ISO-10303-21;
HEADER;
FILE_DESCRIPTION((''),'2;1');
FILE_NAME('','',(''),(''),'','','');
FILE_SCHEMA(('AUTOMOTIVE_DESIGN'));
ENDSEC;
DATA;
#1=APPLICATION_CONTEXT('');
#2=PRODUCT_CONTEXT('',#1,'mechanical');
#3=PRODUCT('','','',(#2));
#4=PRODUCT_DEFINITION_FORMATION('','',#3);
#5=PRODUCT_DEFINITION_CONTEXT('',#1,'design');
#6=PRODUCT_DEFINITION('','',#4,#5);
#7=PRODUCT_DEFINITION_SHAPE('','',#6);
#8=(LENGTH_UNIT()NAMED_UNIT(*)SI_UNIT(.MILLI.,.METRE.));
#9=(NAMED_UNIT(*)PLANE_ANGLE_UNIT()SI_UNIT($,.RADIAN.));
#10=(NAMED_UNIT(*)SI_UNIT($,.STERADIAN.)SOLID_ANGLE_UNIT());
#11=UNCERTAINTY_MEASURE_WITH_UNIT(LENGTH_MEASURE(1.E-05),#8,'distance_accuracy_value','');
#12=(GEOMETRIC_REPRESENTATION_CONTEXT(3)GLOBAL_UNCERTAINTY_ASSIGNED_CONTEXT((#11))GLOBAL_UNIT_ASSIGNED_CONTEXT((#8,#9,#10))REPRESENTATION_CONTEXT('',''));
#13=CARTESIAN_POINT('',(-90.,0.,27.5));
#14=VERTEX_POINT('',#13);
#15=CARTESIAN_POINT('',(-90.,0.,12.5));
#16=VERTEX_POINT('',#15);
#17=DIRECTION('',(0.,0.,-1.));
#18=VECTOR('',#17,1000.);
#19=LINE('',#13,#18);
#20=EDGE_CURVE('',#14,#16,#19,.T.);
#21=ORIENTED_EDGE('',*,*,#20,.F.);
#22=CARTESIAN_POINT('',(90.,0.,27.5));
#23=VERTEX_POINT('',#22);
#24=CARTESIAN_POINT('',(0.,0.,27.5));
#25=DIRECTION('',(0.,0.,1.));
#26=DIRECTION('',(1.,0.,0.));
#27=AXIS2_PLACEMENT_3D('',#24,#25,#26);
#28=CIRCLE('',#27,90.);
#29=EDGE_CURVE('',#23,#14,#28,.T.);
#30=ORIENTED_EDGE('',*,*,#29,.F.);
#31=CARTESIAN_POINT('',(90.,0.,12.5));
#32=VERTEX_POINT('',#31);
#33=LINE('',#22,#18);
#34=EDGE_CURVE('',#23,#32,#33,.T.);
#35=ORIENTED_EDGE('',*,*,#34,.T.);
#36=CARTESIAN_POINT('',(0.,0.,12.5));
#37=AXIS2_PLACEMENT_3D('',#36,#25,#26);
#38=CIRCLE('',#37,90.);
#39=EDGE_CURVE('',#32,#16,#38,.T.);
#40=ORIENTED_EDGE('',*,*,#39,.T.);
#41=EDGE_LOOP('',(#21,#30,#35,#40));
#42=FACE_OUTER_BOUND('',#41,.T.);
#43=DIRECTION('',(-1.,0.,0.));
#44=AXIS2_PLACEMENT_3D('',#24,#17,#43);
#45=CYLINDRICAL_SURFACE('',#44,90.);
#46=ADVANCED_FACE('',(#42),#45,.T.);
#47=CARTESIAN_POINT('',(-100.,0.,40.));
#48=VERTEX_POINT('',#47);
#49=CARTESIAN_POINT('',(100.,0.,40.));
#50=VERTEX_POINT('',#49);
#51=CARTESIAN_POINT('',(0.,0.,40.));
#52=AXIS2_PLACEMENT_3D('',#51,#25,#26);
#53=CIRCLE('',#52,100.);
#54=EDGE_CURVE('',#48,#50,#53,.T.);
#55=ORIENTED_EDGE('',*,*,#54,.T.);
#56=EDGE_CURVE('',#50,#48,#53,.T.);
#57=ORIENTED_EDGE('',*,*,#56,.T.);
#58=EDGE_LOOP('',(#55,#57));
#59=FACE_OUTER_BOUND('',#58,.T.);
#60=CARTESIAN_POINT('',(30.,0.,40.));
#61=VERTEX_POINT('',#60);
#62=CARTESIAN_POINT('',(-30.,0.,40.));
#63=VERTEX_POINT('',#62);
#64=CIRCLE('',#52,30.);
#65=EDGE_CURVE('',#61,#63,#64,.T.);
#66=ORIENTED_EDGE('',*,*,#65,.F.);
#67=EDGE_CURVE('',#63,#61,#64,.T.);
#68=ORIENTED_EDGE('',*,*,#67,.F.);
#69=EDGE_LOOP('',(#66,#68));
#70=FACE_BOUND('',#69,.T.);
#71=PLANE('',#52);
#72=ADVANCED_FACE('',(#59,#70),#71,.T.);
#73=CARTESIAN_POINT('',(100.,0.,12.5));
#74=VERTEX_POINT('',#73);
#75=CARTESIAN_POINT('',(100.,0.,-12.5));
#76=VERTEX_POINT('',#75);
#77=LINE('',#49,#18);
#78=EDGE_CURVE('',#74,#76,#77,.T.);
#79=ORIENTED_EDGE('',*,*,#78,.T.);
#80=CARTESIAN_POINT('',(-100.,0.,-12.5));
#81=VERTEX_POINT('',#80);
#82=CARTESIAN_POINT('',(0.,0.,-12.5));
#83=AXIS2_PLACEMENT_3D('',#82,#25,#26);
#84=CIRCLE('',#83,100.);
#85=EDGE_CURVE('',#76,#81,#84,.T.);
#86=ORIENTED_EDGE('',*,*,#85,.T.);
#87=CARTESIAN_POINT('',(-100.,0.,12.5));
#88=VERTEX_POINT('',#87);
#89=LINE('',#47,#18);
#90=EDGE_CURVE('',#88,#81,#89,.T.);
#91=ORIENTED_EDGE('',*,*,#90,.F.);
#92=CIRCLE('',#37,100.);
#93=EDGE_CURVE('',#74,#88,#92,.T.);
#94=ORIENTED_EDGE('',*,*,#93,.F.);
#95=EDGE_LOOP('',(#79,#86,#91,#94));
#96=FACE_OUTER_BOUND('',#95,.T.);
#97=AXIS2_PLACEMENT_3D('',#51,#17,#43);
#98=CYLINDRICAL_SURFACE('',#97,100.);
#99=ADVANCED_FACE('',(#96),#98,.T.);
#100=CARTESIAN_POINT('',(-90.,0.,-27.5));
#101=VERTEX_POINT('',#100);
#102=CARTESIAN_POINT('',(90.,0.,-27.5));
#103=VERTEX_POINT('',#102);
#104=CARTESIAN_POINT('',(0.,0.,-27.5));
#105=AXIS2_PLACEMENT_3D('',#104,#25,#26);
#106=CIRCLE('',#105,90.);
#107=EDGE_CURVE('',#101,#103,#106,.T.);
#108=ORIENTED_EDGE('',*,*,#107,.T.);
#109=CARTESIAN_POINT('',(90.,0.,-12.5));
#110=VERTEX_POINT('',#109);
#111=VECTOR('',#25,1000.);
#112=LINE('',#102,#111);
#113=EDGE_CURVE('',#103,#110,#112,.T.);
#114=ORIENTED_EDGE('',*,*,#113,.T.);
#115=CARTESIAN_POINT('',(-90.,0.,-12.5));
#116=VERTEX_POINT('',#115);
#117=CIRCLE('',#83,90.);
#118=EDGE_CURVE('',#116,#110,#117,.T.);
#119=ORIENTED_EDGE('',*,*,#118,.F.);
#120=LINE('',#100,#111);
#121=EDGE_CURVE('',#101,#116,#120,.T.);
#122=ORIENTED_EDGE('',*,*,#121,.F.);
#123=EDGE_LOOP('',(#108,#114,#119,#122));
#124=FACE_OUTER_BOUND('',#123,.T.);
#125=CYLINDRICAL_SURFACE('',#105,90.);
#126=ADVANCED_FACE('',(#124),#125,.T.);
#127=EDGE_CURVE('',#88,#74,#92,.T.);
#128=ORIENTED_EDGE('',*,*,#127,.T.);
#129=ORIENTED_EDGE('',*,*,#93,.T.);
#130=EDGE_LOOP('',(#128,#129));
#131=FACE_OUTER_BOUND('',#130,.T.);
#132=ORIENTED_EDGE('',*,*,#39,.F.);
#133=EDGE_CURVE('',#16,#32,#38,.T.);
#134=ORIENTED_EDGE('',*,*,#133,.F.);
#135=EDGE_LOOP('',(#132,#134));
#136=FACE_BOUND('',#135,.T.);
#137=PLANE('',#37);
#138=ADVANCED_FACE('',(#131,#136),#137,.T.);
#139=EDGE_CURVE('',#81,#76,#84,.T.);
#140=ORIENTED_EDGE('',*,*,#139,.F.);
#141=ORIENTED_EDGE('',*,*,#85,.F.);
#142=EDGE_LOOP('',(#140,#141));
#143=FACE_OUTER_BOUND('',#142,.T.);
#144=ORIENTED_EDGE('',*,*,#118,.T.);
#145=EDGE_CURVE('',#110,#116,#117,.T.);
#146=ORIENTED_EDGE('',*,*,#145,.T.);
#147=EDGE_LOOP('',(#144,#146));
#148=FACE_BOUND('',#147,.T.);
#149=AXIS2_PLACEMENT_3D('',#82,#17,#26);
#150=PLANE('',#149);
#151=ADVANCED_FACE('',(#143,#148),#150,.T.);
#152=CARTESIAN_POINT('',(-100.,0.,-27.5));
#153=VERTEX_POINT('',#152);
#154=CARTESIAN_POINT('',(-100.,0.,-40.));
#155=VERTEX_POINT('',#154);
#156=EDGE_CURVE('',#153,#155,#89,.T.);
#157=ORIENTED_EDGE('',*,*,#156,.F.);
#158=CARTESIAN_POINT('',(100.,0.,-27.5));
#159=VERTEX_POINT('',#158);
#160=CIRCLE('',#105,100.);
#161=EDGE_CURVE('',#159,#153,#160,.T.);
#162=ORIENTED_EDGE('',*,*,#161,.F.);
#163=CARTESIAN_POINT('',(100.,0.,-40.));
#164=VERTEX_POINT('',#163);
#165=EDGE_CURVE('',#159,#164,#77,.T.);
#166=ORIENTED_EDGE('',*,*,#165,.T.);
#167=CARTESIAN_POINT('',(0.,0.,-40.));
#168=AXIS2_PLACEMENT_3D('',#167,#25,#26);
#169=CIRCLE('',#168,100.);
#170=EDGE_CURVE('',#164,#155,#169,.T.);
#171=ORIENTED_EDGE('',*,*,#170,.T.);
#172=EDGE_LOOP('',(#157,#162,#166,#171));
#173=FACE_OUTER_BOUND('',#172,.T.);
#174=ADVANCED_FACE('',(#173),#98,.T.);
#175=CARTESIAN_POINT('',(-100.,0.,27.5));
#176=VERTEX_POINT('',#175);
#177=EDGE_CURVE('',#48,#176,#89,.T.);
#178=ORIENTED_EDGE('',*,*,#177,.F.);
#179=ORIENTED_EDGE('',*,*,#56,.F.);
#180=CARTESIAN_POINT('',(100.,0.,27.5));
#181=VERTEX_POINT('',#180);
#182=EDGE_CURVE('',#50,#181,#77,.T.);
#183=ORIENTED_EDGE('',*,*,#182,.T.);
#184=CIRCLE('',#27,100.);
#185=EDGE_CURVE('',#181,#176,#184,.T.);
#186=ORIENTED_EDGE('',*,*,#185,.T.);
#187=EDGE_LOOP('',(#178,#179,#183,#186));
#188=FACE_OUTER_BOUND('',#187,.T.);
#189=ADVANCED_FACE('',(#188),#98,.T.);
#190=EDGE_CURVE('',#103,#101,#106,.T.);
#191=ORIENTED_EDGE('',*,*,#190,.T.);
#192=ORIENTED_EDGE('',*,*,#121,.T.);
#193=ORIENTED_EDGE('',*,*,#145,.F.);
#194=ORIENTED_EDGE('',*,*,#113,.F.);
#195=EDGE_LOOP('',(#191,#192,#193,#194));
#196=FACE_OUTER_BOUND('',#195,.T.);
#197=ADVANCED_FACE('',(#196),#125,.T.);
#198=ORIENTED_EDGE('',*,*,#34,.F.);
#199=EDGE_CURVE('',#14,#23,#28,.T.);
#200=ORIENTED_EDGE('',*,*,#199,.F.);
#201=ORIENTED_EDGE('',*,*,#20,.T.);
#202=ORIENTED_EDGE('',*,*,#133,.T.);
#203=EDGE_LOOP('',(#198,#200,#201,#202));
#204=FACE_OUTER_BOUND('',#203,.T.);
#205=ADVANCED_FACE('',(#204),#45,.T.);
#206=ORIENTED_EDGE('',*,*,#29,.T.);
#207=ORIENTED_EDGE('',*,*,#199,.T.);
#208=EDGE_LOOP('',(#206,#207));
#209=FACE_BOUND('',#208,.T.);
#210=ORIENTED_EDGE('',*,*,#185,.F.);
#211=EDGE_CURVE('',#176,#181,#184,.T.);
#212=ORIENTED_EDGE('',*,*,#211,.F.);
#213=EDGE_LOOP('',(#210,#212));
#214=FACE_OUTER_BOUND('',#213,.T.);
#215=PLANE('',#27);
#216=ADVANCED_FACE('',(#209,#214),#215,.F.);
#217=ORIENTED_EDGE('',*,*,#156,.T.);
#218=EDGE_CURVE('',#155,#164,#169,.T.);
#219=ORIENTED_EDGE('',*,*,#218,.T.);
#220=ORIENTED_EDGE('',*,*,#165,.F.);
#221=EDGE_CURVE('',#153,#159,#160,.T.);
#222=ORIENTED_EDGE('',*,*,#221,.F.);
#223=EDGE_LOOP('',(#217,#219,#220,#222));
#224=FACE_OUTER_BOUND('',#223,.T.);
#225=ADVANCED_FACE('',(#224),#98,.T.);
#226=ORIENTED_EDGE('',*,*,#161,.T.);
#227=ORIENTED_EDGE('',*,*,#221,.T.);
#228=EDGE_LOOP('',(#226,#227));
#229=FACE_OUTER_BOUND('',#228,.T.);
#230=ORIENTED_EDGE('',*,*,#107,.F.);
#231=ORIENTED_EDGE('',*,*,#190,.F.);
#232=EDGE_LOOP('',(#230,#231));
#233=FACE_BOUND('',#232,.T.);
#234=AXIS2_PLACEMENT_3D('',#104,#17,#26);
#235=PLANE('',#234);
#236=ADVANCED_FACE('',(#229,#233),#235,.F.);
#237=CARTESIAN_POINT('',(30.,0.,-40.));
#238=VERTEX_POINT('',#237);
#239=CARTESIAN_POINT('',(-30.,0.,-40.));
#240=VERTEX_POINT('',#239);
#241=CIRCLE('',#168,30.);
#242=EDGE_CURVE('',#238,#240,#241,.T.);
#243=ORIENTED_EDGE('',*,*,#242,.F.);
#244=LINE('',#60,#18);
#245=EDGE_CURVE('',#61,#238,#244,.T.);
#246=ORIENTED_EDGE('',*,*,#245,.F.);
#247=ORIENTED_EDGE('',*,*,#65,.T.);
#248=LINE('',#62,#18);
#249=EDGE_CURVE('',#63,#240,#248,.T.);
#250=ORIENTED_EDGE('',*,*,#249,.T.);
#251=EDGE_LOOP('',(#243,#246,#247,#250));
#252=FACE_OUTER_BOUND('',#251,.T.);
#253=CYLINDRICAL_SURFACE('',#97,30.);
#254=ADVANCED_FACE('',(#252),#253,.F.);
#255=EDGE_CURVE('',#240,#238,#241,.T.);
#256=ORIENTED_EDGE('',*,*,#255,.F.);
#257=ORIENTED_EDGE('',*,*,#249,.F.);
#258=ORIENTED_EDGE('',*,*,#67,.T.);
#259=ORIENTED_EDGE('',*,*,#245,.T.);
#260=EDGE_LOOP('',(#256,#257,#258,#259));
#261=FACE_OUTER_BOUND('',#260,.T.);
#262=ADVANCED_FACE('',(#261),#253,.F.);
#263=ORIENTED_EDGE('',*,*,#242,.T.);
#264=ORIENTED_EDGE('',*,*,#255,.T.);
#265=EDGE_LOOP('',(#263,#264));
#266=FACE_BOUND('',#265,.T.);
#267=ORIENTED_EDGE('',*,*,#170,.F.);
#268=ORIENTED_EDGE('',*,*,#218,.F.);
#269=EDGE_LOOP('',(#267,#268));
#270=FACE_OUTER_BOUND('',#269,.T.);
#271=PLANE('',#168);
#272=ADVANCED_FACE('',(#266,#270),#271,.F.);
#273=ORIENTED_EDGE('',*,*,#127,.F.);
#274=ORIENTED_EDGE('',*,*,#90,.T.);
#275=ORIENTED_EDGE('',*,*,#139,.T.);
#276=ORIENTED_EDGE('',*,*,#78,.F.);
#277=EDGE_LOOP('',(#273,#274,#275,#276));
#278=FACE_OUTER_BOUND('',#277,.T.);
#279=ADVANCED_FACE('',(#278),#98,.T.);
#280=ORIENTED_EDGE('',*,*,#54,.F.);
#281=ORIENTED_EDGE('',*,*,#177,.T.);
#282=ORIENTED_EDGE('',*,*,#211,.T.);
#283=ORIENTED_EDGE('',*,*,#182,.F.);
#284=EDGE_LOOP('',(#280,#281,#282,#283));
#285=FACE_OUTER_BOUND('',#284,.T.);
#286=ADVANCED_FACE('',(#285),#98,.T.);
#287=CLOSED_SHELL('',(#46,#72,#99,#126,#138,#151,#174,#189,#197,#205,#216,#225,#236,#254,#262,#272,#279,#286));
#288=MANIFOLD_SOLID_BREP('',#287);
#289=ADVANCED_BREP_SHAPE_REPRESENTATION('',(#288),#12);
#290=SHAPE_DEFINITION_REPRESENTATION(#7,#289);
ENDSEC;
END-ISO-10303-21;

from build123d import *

# Parameters (mm, degrees)
SKETCH_1_R          = 100
SKETCH_1_R_2        = 30
EXTRUDE_1_DEPTH     = 40
SKETCH_2_R          = 100
SKETCH_2_R_2        = 90
CUT_EXTRUDE_1_DEPTH = 7.5


with BuildPart() as part:
    # 草图1 → 凸台-拉伸1 (new, symmetric)
    with BuildSketch(Plane.XY):
        Circle(SKETCH_1_R)
        Circle(SKETCH_1_R_2, mode=Mode.SUBTRACT)
    extrude(amount=EXTRUDE_1_DEPTH, both=True)

    # 草图2 → 切除-拉伸1 (cut, symmetric)
    with BuildSketch(Plane.XY.offset(20)):
        Circle(SKETCH_2_R)
        Circle(SKETCH_2_R_2, mode=Mode.SUBTRACT)
    cut_extrude_1 = extrude(amount=CUT_EXTRUDE_1_DEPTH, both=True, mode=Mode.SUBTRACT)

    # 镜向1: 切除-拉伸1 across plane
    add(cut_extrude_1.mirror(Plane.XY), mode=Mode.SUBTRACT)


solid = part.part
